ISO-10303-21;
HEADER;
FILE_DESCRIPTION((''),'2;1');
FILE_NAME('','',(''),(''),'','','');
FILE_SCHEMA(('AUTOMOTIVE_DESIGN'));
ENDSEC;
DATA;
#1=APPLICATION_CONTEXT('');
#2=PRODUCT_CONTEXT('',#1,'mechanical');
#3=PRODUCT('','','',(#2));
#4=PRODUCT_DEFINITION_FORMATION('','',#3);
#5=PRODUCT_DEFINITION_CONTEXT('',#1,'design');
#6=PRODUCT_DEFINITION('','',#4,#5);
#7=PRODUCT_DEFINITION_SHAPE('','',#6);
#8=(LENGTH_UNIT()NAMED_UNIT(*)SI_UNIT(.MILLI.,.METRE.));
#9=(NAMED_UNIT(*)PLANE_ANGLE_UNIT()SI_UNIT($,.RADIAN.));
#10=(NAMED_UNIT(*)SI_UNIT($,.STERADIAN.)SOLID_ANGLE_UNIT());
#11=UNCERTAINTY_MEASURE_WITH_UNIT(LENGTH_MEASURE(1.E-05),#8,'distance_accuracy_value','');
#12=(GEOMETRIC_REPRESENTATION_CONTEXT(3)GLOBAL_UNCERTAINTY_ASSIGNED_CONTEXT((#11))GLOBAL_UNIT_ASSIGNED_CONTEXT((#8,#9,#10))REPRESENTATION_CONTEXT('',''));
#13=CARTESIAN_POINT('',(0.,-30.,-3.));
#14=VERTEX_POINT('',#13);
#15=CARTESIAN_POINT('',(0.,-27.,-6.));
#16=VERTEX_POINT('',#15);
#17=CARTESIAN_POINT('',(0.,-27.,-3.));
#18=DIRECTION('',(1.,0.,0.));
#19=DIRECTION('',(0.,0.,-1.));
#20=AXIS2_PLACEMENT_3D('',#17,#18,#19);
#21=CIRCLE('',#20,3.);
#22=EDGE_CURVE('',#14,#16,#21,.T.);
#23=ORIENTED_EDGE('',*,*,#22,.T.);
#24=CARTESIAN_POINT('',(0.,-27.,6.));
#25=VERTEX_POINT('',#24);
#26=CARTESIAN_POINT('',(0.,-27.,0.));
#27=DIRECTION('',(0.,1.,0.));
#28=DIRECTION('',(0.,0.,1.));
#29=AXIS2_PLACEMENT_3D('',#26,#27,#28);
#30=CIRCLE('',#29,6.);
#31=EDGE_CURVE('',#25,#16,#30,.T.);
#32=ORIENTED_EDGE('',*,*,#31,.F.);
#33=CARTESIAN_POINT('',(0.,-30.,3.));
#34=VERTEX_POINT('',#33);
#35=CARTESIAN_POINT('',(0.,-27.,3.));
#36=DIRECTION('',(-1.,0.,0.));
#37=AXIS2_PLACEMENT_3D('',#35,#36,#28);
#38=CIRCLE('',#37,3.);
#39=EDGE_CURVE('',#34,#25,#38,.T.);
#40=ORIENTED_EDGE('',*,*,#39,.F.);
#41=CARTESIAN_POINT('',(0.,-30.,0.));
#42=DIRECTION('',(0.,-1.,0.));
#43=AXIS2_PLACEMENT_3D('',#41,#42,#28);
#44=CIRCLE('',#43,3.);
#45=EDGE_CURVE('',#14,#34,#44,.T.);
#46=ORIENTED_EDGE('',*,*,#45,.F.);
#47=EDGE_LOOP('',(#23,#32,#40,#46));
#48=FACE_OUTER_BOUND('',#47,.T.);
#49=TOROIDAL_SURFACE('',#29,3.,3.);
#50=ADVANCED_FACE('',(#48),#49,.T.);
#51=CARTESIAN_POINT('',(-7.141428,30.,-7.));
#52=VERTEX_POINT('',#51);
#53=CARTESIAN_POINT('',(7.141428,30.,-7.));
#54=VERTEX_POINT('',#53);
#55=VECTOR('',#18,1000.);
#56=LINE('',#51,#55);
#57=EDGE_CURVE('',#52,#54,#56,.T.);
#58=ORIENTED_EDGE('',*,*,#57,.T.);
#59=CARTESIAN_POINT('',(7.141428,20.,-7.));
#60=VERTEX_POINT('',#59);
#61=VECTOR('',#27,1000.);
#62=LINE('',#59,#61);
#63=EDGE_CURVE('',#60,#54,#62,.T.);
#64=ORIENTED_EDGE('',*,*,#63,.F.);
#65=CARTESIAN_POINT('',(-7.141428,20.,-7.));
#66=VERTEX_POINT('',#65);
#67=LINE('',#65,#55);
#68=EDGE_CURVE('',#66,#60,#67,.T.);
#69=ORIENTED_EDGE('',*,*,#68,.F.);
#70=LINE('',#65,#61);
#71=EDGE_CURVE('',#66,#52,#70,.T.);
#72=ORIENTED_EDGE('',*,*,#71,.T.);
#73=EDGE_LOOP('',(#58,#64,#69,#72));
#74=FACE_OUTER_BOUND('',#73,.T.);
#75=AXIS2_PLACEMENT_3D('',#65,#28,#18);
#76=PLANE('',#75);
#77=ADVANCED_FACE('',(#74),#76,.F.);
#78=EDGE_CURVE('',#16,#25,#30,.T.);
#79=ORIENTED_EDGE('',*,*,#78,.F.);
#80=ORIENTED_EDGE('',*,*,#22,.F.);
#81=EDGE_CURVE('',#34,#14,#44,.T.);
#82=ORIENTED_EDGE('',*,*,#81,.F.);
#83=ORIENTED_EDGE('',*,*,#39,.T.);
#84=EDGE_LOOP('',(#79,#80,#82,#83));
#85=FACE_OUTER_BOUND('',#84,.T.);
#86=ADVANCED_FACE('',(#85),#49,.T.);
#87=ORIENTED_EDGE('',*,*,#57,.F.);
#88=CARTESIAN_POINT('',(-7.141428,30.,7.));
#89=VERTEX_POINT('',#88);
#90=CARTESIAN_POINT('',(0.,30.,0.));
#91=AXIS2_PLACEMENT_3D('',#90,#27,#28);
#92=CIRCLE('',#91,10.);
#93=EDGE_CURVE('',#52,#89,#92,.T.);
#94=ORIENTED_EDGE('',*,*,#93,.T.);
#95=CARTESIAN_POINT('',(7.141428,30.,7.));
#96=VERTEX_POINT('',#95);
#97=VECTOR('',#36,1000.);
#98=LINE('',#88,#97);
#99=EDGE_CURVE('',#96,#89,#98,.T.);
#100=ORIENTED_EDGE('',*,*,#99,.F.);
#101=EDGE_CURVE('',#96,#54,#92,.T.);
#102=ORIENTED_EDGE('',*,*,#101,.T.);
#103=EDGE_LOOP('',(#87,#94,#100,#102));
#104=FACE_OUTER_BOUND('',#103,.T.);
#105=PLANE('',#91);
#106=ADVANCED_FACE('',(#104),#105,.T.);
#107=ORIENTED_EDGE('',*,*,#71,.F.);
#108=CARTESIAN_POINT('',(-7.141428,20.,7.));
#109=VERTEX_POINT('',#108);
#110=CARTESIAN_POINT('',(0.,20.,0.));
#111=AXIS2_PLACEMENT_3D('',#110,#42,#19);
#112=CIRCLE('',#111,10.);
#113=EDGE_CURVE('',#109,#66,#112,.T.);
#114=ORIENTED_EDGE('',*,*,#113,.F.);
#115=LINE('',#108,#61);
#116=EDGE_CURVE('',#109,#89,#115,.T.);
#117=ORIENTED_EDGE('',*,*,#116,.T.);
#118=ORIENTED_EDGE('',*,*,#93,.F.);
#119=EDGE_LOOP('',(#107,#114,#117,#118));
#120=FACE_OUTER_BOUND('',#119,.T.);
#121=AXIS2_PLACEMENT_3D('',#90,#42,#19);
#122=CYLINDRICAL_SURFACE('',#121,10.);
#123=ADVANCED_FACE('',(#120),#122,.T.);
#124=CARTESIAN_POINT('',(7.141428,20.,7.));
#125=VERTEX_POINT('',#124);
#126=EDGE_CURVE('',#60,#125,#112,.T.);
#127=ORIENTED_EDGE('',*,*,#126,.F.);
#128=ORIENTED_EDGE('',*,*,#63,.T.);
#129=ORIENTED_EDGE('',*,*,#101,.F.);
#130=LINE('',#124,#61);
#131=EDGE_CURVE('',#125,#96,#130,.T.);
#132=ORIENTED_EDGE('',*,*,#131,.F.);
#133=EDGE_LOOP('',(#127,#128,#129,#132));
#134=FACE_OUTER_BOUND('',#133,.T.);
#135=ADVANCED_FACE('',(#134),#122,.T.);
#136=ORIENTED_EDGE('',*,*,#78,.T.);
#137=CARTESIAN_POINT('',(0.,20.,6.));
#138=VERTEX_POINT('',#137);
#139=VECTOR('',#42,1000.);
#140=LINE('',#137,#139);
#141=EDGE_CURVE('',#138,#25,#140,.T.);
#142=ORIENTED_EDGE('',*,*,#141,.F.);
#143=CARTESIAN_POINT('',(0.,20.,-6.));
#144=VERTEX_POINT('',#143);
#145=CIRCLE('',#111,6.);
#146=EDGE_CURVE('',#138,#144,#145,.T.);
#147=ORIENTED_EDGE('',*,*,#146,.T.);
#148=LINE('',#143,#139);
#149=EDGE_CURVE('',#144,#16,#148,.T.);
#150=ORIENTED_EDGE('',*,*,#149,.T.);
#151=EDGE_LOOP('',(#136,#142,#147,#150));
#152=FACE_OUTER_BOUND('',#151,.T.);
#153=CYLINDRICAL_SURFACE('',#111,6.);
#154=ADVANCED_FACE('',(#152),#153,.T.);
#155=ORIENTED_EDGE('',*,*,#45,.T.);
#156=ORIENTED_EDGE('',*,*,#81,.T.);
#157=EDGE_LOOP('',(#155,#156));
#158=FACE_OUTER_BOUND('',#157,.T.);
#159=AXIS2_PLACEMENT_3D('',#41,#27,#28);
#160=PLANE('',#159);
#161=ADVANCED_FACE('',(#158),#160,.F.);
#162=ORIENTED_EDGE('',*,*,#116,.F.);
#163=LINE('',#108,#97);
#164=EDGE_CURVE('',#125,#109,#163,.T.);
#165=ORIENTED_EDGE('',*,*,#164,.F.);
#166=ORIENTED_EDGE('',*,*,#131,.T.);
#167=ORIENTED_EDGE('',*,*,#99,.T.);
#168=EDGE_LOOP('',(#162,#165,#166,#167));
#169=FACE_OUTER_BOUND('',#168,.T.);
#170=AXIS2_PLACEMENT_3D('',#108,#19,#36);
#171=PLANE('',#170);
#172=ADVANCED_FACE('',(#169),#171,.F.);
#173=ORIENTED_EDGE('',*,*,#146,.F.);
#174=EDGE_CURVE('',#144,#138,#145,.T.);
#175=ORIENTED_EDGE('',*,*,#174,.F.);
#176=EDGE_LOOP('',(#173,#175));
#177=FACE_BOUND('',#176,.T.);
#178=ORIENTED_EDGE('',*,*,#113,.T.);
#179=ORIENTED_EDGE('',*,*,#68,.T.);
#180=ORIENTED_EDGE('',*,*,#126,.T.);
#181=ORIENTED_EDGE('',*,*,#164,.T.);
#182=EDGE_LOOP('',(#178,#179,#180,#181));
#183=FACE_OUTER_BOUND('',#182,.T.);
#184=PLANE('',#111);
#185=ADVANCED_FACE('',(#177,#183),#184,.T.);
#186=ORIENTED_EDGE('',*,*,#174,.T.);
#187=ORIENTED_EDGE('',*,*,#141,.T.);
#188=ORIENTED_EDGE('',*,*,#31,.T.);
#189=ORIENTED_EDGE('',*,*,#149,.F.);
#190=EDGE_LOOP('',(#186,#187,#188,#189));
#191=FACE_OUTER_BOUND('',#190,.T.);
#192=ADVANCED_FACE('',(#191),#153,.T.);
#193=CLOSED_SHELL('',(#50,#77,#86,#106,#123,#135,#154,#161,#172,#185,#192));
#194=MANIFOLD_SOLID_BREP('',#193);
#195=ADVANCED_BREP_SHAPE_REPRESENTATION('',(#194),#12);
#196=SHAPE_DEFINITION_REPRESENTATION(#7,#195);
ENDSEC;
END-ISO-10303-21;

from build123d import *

# Parameters (mm, degrees)
SKETCH_1_R          = 10
EXTRUDE_1_DEPTH     = 30
CUT_EXTRUDE_START   = -50
SKETCH_2_R          = 10
SKETCH_2_R_2        = 6
CUT_EXTRUDE_1_DEPTH = 50
FILLET_1_R          = 3
CUT_EXTRUDE_3_DEPTH = 10


with BuildPart() as part:
    # 草图1 → 凸台-拉伸1 (new, symmetric)
    with BuildSketch(Plane(origin=(0, 0, 0), x_dir=(1, 0, 0), z_dir=(0, 1, 0))):
        with Locations(Location((0, 0, 0), (0, 0, 270))):
            Circle(SKETCH_1_R)
    extrude(amount=EXTRUDE_1_DEPTH, both=True)

    # 草图2 → 切除-拉伸1 (cut)
    with BuildSketch(Plane.XZ.offset(30).offset(CUT_EXTRUDE_START)):
        with Locations(Location((0, 0, 0), (0, 0, 270))):
            Circle(SKETCH_2_R)
        with Locations(Location((0, 0, 0), (0, 0, 270))):
            Circle(SKETCH_2_R_2, mode=Mode.SUBTRACT)
    extrude(amount=CUT_EXTRUDE_1_DEPTH, mode=Mode.SUBTRACT)

    # 圆角1
    fillet_1_edges = [part.edges().sort_by_distance(p)[0] for p in [
        (0, -30, 6),
    ]]
    fillet(fillet_1_edges, radius=FILLET_1_R)

    # 草图3 → 切除-拉伸3 (cut)
    with BuildSketch(Plane(origin=(0, 30, 0), x_dir=(1, 0, 0), z_dir=(0, 1, 0))):
        with BuildLine():
            Line((-7.141428429, 7), (7.141428429, 7))
            ThreePointArc((7.141428429, 7), (0, 10), (-7.141428429, 7))
        make_face()
        with BuildLine():
            Line((-7.141428429, -7), (7.141428429, -7))
            ThreePointArc((7.141428429, -7), (0, -10), (-7.141428429, -7))
        make_face()
    extrude(amount=-CUT_EXTRUDE_3_DEPTH, mode=Mode.SUBTRACT)


solid = part.part
